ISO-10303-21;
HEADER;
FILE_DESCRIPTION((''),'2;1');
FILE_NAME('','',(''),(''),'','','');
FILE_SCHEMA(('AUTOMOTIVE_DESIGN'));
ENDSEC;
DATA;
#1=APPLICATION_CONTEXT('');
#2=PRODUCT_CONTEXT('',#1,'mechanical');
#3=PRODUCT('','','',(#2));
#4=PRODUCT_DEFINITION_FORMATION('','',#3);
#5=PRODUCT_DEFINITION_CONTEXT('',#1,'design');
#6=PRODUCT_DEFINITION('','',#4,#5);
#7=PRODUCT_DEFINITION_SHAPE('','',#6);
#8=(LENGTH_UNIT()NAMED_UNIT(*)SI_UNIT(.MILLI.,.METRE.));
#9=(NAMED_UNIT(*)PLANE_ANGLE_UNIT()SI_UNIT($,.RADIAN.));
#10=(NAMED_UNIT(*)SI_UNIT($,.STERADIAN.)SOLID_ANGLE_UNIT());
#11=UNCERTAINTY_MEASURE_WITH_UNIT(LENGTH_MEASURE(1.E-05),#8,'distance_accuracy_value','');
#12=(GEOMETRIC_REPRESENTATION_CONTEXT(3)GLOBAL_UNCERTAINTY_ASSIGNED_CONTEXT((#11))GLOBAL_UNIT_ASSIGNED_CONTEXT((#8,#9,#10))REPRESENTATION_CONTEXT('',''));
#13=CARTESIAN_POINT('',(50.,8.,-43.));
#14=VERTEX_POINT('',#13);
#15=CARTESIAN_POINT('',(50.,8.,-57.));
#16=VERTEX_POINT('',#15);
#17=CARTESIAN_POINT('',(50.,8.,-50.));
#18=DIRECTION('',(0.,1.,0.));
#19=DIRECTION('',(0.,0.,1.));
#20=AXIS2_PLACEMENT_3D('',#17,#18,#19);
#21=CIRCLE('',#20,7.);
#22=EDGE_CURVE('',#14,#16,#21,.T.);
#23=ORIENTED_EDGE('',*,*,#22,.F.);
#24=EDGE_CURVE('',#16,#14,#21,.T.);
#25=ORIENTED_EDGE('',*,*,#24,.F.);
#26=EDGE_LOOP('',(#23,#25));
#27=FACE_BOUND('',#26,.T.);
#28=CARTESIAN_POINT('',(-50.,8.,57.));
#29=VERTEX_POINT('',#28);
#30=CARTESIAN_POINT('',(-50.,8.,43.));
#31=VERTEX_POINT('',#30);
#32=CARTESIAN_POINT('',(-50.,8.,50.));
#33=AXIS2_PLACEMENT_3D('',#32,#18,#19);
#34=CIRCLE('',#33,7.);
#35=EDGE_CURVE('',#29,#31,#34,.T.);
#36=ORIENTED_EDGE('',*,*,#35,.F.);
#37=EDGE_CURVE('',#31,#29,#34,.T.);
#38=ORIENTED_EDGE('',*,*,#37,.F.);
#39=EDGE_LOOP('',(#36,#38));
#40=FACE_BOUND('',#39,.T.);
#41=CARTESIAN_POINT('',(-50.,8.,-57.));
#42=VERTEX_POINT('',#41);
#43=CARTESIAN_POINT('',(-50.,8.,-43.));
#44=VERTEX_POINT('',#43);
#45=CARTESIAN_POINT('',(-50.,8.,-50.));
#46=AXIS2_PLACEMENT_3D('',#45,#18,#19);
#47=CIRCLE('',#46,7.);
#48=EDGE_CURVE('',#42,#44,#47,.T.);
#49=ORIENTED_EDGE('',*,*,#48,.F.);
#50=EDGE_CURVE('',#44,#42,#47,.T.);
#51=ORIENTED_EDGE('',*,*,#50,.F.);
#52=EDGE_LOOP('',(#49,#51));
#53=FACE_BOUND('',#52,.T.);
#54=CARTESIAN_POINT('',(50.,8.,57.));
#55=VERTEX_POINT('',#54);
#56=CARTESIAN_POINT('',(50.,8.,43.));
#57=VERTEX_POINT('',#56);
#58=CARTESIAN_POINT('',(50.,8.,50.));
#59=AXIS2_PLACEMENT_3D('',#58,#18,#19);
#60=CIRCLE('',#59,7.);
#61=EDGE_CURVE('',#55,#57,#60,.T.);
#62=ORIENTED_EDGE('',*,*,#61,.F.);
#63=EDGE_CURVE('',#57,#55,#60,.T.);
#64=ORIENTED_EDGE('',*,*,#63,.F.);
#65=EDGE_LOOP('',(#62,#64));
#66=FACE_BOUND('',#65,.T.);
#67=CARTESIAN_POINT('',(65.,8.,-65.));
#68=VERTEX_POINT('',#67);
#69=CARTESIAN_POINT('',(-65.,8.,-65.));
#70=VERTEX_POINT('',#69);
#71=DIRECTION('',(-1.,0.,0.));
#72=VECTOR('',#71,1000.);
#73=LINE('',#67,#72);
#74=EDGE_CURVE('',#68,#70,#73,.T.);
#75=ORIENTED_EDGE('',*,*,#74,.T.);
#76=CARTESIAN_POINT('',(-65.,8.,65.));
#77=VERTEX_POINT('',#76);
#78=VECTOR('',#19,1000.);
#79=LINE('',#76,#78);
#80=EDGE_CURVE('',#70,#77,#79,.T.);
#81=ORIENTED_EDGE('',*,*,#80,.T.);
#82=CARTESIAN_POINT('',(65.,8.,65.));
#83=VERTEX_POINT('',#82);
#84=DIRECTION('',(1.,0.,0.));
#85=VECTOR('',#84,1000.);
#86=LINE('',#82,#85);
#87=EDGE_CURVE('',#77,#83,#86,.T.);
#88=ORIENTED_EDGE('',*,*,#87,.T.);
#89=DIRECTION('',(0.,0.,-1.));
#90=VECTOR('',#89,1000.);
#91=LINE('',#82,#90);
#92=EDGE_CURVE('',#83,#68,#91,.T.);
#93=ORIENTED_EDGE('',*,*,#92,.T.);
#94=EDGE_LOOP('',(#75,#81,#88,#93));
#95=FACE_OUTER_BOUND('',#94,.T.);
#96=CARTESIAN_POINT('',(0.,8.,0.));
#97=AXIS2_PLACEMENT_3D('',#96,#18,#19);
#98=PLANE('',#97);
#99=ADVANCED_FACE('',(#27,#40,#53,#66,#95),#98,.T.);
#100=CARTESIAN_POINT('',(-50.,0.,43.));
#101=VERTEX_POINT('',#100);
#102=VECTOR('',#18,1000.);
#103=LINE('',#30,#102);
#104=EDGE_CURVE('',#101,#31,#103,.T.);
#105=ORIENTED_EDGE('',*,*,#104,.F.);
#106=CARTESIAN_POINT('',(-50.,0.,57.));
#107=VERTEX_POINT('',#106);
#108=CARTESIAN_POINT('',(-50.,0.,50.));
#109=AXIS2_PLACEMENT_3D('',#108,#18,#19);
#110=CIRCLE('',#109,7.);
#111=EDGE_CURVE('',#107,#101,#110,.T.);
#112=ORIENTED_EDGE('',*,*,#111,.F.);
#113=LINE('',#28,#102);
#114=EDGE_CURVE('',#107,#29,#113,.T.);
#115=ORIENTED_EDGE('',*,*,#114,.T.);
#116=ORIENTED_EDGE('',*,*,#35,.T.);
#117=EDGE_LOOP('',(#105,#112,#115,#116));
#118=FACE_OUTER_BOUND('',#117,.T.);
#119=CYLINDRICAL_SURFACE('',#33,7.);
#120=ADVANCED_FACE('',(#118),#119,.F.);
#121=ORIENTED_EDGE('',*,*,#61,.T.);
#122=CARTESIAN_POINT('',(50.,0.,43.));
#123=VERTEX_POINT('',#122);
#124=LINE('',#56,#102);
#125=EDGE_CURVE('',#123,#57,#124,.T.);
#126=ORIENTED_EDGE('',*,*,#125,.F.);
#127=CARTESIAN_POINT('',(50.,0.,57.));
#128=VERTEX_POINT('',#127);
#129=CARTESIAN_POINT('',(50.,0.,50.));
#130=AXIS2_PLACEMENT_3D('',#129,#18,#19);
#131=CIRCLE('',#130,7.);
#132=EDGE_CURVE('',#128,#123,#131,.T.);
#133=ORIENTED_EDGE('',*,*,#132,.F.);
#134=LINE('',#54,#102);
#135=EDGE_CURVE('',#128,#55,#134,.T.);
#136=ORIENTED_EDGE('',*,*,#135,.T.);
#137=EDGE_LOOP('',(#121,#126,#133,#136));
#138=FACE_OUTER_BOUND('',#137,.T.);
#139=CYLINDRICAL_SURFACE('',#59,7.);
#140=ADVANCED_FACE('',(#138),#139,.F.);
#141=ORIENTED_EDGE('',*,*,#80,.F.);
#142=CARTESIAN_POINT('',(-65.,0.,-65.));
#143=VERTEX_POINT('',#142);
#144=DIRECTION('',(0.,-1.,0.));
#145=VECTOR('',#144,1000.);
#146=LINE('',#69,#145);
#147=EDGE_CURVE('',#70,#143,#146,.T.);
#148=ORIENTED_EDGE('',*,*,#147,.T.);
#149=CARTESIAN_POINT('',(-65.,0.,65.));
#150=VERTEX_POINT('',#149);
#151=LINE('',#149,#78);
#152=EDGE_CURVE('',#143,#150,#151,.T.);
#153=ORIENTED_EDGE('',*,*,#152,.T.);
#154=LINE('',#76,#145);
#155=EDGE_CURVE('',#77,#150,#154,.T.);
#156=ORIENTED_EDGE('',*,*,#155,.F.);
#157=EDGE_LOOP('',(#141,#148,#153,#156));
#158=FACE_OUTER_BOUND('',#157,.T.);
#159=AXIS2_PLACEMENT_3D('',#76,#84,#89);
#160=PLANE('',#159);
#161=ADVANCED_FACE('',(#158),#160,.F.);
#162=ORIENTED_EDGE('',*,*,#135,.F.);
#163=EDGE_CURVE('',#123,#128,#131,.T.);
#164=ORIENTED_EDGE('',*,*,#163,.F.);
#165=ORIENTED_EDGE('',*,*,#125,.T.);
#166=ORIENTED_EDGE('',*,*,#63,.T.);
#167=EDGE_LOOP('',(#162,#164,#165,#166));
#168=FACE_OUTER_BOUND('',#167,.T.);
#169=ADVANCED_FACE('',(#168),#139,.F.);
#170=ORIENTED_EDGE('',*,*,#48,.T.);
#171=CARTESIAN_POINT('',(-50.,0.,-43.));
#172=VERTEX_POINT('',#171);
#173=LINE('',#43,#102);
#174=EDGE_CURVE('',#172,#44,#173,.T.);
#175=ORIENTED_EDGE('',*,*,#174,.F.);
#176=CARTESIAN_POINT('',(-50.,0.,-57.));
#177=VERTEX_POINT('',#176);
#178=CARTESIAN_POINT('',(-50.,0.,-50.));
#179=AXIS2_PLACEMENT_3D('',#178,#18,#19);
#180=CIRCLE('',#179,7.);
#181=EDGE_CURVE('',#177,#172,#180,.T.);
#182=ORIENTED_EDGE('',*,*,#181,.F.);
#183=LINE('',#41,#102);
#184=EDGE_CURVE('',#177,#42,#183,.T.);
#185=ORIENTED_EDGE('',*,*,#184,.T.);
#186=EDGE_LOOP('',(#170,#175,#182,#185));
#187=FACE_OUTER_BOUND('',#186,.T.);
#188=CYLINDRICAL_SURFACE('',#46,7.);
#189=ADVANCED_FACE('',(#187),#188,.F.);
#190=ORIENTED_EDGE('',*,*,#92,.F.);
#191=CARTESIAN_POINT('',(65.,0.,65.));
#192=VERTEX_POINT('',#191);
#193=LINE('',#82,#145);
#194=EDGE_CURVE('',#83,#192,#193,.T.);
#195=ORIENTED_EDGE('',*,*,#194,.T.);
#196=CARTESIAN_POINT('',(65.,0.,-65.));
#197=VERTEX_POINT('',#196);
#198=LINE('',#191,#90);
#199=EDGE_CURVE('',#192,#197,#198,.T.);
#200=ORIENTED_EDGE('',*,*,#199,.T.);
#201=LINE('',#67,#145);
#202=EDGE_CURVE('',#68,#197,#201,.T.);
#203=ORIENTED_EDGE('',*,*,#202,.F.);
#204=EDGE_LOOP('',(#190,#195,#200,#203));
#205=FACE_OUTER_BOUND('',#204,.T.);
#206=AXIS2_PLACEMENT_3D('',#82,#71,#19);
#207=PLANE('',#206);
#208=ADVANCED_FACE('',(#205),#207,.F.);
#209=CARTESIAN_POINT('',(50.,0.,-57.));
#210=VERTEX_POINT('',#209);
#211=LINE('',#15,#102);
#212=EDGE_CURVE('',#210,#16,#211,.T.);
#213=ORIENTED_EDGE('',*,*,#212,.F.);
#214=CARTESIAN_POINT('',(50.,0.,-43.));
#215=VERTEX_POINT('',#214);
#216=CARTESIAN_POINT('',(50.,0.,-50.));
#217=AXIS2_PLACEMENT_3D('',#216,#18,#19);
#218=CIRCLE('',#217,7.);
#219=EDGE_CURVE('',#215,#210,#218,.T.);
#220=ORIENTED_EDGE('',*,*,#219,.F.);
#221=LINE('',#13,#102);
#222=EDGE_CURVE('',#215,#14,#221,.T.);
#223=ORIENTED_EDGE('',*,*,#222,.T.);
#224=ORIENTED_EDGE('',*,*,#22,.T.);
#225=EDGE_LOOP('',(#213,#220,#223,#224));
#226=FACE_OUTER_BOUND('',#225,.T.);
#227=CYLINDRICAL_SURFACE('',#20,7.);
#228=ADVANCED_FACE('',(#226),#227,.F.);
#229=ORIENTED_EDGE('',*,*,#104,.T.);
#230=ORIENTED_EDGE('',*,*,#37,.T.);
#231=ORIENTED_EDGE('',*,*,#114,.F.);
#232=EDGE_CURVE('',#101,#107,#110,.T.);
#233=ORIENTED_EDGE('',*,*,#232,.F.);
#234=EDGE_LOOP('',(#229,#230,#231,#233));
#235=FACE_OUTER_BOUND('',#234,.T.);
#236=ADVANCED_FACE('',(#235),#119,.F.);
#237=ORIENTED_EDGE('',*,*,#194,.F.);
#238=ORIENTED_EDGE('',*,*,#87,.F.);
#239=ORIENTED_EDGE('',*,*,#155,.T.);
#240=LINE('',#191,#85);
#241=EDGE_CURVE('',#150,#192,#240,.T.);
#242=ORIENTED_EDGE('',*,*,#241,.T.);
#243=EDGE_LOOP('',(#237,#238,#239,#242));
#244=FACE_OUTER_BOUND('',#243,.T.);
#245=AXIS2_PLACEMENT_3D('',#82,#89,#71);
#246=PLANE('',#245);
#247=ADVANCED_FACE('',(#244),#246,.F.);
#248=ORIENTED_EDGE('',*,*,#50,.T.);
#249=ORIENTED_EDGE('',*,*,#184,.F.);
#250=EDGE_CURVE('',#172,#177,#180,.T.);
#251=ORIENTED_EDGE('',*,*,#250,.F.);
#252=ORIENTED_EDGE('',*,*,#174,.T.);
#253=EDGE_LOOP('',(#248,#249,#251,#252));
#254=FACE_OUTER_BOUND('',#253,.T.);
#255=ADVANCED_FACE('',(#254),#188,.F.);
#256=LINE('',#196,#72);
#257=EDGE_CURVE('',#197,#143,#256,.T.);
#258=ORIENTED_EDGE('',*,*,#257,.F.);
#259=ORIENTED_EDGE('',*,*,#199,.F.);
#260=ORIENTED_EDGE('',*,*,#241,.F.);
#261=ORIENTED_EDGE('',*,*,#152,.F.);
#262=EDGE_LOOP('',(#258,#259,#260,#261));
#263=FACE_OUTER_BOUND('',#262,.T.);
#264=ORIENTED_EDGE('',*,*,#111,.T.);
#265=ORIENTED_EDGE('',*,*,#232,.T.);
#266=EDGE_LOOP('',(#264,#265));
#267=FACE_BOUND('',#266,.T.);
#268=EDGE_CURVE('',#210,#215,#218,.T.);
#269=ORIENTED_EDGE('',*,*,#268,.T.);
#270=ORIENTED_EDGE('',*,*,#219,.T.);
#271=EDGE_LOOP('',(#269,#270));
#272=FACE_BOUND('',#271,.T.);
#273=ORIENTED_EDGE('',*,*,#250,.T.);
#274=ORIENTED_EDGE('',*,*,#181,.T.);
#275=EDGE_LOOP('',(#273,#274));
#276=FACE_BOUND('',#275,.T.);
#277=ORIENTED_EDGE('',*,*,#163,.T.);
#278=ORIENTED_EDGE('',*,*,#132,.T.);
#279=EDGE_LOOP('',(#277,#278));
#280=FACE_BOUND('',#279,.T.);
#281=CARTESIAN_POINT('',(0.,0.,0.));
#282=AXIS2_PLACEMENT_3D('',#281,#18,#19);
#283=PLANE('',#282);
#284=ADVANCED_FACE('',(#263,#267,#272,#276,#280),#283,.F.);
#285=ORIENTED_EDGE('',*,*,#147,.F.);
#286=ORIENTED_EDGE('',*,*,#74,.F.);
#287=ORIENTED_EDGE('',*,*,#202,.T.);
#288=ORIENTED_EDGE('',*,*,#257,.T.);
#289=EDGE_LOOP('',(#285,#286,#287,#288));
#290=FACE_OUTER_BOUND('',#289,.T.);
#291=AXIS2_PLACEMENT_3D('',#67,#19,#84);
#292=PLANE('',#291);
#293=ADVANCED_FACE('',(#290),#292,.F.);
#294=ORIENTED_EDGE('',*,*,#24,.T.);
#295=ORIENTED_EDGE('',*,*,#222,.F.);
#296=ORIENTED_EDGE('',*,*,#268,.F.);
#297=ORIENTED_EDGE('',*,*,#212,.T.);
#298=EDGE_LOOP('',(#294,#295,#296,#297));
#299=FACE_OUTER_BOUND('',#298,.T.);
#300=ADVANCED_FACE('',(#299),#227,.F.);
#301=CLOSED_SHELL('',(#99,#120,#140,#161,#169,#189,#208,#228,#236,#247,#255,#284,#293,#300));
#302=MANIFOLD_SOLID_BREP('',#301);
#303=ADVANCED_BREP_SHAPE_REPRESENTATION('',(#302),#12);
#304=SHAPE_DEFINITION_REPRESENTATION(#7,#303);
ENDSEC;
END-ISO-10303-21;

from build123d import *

# Parameters (mm, degrees)
SKETCH1_W                  = 130
SKETCH1_H                  = 130
BOSS_EXTRUDE1_DEPTH        = 8
F_14_0_14_DIAMETER_HOLE1_D = 14


with BuildPart() as part:
    # Sketch1 → Boss-Extrude1 (new body)
    with BuildSketch(Plane(origin=(0, 0, 0), x_dir=(1, 0, 0), z_dir=(0, 1, 0))):
        Rectangle(SKETCH1_W, SKETCH1_H)
    extrude(amount=BOSS_EXTRUDE1_DEPTH)

    # Ø14.0 (14) Diameter Hole1 (through all)
    with Locations(Plane(origin=(0, 8, 0), x_dir=(1, 0, 0), z_dir=(0, 1, 0))):
        with Locations((-50, -50), (50, -50), (50, 50), (-50, 50)):
            Hole(F_14_0_14_DIAMETER_HOLE1_D / 2)


solid = part.part
